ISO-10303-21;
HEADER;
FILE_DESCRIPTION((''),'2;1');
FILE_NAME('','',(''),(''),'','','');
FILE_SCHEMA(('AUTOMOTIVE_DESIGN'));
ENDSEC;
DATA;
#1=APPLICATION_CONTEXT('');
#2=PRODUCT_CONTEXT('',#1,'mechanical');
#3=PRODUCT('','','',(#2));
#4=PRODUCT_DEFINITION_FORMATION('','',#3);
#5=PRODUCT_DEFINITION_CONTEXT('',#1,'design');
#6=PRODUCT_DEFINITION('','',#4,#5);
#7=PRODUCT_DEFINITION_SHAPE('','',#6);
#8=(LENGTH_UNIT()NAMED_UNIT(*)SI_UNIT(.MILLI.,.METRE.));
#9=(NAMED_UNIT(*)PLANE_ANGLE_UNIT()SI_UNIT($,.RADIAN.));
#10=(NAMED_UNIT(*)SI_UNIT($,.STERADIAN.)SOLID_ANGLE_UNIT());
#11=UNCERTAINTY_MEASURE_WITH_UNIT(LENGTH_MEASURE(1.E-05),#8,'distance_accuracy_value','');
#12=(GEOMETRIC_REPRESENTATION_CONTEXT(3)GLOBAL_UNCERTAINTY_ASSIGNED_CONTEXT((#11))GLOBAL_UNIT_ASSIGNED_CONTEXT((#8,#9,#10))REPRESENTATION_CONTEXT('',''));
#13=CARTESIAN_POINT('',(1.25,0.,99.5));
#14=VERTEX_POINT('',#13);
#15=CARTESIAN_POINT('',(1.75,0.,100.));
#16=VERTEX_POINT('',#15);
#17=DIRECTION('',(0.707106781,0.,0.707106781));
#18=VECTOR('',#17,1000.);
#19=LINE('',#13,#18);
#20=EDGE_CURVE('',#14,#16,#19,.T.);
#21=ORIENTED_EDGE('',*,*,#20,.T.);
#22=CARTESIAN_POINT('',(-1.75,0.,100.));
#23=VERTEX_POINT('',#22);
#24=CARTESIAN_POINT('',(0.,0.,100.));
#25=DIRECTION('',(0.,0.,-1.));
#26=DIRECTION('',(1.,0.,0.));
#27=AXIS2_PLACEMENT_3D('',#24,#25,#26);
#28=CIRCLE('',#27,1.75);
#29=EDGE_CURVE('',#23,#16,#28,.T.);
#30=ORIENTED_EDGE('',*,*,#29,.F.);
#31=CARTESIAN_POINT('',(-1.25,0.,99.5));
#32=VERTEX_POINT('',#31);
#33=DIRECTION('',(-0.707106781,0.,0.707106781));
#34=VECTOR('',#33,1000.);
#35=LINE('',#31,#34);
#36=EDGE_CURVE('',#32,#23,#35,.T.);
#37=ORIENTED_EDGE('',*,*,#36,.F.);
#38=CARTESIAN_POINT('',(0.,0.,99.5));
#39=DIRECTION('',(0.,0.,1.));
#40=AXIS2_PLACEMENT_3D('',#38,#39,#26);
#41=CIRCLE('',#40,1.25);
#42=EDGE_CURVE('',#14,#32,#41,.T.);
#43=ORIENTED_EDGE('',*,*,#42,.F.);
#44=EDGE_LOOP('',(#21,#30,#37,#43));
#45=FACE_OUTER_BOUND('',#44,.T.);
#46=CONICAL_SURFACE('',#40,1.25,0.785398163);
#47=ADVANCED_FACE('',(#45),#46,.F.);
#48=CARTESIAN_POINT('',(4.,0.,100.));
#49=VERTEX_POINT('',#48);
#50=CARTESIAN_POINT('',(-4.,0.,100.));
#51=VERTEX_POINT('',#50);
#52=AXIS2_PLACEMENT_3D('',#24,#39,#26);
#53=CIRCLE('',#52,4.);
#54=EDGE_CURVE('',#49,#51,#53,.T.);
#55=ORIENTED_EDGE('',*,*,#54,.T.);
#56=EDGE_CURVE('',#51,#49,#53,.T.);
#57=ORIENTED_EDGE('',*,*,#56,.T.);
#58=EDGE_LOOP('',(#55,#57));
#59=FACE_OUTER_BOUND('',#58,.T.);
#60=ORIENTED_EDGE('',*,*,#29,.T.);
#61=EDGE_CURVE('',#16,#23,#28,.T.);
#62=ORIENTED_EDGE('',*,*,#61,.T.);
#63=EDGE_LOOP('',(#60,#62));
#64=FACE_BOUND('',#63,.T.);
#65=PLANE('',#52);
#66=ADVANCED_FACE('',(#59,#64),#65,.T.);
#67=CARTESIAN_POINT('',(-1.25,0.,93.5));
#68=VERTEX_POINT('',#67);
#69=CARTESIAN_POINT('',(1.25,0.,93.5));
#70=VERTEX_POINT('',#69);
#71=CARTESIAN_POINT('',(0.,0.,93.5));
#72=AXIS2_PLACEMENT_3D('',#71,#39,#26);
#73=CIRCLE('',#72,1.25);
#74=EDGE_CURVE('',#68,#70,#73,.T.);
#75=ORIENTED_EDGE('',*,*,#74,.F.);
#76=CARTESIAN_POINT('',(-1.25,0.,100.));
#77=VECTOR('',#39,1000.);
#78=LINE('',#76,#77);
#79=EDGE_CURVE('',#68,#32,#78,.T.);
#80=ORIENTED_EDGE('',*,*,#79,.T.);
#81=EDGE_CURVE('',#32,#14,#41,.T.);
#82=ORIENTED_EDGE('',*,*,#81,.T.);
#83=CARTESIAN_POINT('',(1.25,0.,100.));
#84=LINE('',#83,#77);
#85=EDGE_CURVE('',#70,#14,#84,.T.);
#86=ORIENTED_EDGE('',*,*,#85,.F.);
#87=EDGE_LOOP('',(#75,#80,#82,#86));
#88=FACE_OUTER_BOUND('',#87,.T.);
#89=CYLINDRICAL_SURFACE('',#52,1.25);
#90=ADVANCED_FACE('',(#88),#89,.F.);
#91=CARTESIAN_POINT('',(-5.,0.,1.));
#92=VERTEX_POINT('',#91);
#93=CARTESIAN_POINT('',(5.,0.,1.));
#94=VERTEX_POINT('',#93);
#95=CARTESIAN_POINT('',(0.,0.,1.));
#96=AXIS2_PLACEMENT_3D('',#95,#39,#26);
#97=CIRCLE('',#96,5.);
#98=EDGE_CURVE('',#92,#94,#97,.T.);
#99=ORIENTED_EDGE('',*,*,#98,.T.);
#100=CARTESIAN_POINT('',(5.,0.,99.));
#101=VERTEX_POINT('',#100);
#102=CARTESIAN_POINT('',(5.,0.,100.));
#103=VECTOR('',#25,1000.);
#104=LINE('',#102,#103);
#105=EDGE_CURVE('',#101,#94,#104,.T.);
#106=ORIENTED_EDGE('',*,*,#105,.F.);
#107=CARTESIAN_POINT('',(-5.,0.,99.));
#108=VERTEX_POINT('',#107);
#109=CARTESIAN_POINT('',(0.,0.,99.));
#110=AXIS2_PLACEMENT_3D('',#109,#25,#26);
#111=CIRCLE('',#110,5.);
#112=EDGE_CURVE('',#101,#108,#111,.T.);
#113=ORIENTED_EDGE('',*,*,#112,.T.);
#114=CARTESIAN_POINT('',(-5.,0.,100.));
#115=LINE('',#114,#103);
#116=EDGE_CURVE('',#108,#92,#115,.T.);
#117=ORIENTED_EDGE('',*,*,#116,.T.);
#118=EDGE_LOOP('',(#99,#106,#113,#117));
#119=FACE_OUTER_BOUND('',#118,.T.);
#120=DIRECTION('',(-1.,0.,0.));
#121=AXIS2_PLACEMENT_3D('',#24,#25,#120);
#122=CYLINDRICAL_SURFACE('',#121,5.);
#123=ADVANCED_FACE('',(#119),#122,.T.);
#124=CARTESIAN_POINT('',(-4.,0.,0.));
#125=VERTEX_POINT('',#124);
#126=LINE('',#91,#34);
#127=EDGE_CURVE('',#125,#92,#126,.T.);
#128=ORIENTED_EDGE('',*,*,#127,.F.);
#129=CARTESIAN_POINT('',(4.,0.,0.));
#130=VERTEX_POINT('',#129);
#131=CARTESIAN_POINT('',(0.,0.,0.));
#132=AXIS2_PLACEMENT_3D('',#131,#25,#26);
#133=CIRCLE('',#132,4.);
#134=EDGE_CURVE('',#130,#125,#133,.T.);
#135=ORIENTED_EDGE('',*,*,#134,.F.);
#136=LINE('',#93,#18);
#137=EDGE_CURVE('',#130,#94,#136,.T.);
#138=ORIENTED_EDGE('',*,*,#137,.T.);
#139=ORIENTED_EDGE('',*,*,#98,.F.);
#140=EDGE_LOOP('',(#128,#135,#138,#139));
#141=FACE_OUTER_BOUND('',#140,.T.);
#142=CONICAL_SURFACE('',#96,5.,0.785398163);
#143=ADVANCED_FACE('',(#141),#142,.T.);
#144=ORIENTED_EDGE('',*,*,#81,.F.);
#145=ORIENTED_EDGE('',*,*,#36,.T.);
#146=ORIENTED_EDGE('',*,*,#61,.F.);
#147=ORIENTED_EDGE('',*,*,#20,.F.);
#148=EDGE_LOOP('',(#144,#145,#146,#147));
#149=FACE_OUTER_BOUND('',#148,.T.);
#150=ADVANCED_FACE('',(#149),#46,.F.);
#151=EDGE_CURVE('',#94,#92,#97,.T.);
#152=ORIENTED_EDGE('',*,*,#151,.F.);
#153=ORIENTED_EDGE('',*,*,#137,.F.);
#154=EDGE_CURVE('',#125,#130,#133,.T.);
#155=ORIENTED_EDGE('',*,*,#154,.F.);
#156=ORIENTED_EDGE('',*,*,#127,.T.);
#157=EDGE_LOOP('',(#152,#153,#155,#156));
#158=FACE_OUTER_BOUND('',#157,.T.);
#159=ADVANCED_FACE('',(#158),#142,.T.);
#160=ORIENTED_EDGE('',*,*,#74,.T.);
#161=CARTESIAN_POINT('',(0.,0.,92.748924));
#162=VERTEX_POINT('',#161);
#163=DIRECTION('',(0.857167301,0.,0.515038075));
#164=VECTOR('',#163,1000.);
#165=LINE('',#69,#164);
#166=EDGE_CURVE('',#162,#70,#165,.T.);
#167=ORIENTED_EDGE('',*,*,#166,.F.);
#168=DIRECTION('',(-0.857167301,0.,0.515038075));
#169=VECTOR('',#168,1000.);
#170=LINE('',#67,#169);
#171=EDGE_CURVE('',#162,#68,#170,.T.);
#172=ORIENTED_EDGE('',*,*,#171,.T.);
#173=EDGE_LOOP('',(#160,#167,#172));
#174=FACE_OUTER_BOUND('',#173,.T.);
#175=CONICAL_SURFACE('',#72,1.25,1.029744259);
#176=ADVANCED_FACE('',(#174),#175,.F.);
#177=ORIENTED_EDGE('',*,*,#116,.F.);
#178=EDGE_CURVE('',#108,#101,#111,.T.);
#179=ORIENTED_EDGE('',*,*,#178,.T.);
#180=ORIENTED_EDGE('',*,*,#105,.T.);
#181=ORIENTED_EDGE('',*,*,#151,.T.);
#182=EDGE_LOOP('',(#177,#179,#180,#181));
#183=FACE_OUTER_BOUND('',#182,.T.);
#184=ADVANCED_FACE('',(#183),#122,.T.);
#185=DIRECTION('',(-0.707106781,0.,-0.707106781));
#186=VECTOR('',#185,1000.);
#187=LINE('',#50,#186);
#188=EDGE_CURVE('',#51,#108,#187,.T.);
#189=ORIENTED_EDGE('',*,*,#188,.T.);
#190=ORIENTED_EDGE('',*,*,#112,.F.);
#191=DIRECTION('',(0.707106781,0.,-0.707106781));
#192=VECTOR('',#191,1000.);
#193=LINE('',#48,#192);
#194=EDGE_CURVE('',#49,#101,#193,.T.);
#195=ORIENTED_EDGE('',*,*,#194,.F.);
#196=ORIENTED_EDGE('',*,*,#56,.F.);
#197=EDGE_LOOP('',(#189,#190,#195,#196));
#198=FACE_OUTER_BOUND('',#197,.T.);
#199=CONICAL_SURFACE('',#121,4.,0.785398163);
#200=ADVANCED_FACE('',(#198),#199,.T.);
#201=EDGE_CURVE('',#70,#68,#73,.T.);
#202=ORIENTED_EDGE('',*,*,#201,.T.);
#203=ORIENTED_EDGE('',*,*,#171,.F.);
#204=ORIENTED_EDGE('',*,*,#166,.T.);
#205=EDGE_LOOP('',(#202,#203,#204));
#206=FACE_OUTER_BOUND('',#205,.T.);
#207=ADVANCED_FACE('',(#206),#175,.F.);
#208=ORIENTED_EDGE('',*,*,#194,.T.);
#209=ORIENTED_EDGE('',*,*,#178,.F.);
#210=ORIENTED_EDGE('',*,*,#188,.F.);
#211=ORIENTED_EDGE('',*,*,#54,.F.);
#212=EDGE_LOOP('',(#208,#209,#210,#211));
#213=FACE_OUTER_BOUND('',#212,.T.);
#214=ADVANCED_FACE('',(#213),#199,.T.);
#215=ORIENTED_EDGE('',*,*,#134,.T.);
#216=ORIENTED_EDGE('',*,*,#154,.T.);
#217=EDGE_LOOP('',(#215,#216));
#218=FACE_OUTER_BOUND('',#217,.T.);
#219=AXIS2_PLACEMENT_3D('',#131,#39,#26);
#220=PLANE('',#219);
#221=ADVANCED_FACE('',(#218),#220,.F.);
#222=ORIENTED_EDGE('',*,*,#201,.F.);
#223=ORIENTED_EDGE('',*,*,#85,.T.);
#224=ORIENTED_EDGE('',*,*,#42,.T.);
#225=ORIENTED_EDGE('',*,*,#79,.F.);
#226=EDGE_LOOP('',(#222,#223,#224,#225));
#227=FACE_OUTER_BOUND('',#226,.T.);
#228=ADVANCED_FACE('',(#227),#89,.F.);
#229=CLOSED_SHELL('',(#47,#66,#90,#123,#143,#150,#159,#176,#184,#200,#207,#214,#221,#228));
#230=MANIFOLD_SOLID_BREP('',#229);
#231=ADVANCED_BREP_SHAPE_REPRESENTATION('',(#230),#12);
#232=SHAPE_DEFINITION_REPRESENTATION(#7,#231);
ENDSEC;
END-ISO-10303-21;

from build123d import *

# Parameters (mm, degrees)
SKETCH1_R             = 5
BOSS_EXTRUDE1_DEPTH   = 100
M3_TAPPED_HOLE1_D     = 2.5
M3_TAPPED_HOLE1_DEPTH = 6.5
M3_TAPPED_HOLE1_TIP   = 0.751075774
CHAMFER1_SIZE         = 1
CHAMFER2_SIZE         = 0.5


with BuildPart() as part:
    # Sketch1 → Boss-Extrude1 (new body)
    with BuildSketch(Plane.XY):
        Circle(SKETCH1_R)
    extrude(amount=BOSS_EXTRUDE1_DEPTH)

    # M3 Tapped Hole1
    with Locations(Plane.XY.offset(100)):
        with Locations((0, 0)):
            Hole(M3_TAPPED_HOLE1_D / 2, depth=M3_TAPPED_HOLE1_DEPTH)
            with Locations((0, 0, -(M3_TAPPED_HOLE1_DEPTH + M3_TAPPED_HOLE1_TIP / 2))):  # 118° drill point
                Cone(0, M3_TAPPED_HOLE1_D / 2, M3_TAPPED_HOLE1_TIP, mode=Mode.SUBTRACT)

    # Chamfer1
    chamfer1_edges = [part.edges().sort_by_distance(p)[0] for p in [
        (-5, 0, 0),
        (-5, 0, 100),
    ]]
    chamfer(chamfer1_edges, length=CHAMFER1_SIZE)

    # Chamfer2
    chamfer2_edges = [part.edges().sort_by_distance(p)[0] for p in [
        (1.25, 0, 100),
    ]]
    chamfer(chamfer2_edges, length=CHAMFER2_SIZE)


solid = part.part
